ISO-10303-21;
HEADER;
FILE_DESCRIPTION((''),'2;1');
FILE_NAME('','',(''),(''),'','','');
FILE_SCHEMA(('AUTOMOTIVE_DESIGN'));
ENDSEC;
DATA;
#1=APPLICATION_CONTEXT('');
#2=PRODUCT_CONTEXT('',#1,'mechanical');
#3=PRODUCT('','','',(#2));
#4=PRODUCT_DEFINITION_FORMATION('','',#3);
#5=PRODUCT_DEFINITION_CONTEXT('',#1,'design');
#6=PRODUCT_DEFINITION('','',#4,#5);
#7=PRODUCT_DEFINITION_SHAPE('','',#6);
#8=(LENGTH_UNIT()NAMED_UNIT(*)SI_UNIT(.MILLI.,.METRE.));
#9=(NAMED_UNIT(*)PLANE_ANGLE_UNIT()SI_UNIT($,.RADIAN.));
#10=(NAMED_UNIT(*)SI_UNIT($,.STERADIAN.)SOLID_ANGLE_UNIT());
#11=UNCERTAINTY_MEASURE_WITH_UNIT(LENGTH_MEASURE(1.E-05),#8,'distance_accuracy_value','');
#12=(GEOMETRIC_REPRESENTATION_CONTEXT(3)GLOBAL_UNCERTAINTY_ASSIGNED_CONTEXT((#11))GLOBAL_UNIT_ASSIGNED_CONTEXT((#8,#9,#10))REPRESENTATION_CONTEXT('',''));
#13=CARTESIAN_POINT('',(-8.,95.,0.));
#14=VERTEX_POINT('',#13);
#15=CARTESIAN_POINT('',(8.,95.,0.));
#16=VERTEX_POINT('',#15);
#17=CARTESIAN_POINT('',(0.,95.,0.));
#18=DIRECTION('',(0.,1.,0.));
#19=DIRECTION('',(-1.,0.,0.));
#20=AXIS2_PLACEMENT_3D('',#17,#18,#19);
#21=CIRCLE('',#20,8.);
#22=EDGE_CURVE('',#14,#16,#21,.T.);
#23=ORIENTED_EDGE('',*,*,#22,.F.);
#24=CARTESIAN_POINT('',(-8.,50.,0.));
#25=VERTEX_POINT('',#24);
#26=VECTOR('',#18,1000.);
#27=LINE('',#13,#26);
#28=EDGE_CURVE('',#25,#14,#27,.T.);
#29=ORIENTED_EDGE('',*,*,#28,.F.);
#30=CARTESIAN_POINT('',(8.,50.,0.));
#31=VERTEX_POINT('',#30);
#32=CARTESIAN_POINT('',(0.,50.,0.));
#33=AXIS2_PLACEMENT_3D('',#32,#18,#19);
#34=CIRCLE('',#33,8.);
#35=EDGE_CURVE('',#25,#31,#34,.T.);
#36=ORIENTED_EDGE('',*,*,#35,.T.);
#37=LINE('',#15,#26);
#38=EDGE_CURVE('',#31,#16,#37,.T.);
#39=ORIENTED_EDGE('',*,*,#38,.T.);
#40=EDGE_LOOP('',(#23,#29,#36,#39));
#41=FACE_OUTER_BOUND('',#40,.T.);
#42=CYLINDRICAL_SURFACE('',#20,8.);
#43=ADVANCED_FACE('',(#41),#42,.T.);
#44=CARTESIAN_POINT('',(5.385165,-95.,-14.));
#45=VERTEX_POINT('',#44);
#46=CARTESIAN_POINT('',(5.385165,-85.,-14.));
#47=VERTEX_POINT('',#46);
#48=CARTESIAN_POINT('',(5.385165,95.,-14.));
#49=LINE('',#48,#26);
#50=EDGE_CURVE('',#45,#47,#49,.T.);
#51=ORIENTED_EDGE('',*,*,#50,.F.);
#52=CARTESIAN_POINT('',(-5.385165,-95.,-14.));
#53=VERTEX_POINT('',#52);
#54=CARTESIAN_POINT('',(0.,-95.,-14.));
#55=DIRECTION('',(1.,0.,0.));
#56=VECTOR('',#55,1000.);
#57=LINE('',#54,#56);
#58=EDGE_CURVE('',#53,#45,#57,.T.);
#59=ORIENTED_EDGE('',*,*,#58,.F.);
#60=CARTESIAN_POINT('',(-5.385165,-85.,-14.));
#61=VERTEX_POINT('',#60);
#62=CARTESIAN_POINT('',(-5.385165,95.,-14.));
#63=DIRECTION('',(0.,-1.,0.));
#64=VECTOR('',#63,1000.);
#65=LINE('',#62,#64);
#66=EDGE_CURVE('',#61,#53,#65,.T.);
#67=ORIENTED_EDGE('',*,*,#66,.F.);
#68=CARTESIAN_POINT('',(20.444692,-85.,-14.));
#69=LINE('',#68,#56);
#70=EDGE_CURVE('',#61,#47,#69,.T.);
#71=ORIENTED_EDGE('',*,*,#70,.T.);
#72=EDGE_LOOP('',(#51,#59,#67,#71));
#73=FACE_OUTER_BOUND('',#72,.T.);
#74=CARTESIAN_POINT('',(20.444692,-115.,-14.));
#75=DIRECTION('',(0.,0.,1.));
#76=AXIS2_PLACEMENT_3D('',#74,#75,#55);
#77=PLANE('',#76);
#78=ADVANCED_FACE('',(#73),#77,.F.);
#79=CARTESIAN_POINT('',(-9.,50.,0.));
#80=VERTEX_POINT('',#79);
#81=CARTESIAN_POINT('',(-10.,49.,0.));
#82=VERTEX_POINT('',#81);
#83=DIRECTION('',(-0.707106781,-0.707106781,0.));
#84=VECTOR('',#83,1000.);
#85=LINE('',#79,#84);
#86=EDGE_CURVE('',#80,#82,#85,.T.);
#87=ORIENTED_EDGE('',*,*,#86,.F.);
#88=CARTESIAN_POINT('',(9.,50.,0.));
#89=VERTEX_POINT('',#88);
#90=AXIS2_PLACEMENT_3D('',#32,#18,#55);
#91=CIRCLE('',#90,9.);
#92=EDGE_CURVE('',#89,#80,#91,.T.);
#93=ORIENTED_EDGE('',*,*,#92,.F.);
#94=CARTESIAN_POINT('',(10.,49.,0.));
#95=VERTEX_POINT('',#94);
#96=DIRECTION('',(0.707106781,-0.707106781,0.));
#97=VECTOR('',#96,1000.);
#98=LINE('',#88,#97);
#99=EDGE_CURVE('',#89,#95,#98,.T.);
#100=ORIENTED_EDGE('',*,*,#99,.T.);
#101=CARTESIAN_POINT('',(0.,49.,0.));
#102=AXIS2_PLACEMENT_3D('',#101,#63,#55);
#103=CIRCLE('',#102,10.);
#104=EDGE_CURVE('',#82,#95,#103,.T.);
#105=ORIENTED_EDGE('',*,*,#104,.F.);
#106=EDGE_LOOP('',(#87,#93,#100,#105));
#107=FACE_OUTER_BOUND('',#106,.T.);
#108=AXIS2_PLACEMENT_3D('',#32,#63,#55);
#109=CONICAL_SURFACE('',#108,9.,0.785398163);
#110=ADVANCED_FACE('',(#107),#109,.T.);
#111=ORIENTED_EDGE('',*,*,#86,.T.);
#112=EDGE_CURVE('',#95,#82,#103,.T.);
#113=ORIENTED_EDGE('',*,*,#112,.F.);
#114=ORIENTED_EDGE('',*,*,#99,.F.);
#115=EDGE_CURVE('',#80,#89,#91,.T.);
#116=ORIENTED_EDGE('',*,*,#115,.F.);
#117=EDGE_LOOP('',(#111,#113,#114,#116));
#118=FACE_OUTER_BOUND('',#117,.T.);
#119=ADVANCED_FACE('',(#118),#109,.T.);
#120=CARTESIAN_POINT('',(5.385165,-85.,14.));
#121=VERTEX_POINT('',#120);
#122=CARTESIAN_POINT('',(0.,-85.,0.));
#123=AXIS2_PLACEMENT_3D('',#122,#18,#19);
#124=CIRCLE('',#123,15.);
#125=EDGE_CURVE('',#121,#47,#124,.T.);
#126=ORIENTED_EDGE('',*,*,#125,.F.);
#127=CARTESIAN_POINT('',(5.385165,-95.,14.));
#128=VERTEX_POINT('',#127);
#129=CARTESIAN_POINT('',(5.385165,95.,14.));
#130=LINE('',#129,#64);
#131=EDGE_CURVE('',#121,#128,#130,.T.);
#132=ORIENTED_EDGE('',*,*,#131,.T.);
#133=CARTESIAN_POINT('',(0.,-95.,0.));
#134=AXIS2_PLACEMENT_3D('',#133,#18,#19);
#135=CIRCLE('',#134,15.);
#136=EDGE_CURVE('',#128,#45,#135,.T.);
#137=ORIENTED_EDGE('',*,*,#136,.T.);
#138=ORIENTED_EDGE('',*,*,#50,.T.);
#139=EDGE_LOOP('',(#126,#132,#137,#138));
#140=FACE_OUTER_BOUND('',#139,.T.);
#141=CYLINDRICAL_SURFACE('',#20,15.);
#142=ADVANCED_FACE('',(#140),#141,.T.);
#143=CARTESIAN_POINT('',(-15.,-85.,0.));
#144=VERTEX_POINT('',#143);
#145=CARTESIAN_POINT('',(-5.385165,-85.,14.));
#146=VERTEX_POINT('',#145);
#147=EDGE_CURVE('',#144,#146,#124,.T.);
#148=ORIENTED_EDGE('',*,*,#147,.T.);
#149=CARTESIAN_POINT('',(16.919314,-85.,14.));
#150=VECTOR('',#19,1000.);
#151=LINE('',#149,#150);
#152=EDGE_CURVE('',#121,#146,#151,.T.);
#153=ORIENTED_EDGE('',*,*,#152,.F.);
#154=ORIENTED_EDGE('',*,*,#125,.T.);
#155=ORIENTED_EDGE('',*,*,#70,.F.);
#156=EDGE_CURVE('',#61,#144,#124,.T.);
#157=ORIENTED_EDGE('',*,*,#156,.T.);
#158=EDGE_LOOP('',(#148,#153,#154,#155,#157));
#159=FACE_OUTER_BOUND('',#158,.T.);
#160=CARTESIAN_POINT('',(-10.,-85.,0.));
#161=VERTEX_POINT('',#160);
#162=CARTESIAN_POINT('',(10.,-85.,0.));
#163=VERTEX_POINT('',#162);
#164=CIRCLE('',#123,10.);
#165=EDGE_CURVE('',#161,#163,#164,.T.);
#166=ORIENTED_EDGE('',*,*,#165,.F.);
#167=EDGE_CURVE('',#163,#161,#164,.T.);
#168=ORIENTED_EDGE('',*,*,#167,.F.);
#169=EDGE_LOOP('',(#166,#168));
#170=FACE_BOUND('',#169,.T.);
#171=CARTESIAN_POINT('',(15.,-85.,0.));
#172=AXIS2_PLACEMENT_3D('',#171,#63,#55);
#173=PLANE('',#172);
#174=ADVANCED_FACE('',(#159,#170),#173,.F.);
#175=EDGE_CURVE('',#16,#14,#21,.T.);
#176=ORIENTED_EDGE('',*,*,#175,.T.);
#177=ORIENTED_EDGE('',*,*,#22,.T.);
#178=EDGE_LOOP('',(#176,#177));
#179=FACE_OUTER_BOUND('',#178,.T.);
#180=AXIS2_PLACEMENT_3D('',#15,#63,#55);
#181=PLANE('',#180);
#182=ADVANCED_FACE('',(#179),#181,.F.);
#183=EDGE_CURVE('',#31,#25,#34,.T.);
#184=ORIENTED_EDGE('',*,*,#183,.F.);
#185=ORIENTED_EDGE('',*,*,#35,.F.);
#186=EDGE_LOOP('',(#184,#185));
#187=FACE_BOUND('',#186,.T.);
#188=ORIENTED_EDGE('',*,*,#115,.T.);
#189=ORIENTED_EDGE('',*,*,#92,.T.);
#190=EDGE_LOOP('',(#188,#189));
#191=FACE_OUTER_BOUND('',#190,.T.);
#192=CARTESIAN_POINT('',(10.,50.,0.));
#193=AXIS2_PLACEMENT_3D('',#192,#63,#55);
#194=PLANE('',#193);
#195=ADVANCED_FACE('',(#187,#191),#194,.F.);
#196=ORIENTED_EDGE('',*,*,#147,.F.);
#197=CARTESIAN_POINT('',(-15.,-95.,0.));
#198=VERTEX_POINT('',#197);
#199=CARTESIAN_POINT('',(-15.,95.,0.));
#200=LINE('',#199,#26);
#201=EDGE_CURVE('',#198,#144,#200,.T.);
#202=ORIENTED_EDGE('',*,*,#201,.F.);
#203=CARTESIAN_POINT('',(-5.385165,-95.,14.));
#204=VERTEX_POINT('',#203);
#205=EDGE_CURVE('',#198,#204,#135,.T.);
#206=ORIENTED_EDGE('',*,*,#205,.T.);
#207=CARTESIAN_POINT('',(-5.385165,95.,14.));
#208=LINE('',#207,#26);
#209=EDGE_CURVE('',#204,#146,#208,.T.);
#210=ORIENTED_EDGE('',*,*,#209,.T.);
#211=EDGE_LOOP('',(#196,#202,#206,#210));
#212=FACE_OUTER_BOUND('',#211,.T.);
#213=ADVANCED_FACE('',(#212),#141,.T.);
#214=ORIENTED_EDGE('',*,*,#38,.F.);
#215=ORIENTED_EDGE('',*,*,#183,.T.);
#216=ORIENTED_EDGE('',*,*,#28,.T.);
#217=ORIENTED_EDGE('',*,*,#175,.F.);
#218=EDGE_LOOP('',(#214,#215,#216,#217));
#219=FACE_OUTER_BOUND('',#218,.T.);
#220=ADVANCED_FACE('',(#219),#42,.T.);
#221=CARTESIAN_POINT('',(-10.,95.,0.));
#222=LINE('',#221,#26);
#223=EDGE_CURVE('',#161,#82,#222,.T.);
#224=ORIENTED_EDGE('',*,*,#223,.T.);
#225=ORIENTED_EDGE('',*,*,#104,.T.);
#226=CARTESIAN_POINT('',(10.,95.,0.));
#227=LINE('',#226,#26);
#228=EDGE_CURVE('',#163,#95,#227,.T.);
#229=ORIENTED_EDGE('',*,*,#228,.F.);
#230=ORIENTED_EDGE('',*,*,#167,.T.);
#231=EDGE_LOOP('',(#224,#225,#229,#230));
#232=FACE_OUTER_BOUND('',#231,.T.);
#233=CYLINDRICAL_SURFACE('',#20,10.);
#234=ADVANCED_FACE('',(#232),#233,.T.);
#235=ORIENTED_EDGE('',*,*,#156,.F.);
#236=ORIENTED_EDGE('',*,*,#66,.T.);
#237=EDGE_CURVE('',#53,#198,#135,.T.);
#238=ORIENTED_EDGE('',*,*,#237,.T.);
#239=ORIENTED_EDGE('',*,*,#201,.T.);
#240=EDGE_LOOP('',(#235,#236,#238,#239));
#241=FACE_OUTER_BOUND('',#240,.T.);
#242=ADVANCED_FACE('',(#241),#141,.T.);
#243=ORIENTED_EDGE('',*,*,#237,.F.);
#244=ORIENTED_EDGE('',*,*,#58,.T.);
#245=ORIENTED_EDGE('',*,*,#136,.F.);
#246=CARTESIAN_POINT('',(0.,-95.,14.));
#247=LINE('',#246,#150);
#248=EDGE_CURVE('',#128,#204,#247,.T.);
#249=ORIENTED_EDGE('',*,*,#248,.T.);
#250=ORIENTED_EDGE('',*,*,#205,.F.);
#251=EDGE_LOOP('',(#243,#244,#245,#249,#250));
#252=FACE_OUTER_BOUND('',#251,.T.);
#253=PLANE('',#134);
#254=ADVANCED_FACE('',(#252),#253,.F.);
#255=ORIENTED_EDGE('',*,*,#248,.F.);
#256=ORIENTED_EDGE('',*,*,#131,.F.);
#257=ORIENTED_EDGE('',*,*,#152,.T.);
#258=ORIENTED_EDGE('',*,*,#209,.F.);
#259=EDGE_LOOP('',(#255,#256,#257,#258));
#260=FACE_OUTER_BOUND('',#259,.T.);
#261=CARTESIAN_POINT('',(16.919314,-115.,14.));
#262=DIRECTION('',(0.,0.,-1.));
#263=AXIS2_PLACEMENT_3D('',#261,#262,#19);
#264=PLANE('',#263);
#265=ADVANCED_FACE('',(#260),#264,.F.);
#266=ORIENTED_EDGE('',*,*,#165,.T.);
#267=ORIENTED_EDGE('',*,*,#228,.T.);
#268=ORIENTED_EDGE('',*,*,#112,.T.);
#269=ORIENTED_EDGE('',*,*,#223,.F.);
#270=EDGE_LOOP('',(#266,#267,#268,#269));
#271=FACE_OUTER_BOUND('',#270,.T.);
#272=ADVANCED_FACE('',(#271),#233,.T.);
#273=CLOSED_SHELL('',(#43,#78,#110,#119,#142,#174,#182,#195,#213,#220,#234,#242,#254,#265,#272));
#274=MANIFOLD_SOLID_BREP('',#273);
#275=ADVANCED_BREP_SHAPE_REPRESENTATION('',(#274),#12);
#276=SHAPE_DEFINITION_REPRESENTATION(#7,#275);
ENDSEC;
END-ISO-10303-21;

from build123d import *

# Parameters (mm, degrees)
CHAMFER_1_SIZE      = 1
SKETCH_2_W          = 36.885897288
SKETCH_2_H          = 4.926272709
SKETCH_2_W_2        = 40.411275082
SKETCH_2_H_2        = 4.776597597
CUT_EXTRUDE_1_DEPTH = 30


with BuildPart() as part:
    # 草图1 → 旋转1 (revolve)
    with BuildSketch(Plane.XY, mode=Mode.PRIVATE) as revolve_1_sk:
        Polygon((0, 95), (0, -95), (15, -95), (15, -85), (10, -85), (10, 50), (8, 50), (8, 95), align=None)
    revolve(revolve_1_sk.sketch.rotate(Axis((0, 95, 0), (0, -1, 0)), 180), axis=Axis((0, 95, 0), (0, -1, 0)))

    # 倒角1
    chamfer_1_edges = [part.edges().sort_by_distance(p)[0] for p in [
        (10, 50, 0),
    ]]
    chamfer(chamfer_1_edges, length=CHAMFER_1_SIZE)

    # 草图2 → 切除-拉伸1 (cut)
    with BuildSketch(Plane(origin=(0, -85, 0), x_dir=(1, 0, 0), z_dir=(0, 1, 0))):
        with Locations((-1.52363424, -16.463136355)):
            Rectangle(SKETCH_2_W, SKETCH_2_H)
        with Locations((0.239054657, 16.388298799)):
            Rectangle(SKETCH_2_W_2, SKETCH_2_H_2)
    extrude(amount=-CUT_EXTRUDE_1_DEPTH, mode=Mode.SUBTRACT)


solid = part.part
